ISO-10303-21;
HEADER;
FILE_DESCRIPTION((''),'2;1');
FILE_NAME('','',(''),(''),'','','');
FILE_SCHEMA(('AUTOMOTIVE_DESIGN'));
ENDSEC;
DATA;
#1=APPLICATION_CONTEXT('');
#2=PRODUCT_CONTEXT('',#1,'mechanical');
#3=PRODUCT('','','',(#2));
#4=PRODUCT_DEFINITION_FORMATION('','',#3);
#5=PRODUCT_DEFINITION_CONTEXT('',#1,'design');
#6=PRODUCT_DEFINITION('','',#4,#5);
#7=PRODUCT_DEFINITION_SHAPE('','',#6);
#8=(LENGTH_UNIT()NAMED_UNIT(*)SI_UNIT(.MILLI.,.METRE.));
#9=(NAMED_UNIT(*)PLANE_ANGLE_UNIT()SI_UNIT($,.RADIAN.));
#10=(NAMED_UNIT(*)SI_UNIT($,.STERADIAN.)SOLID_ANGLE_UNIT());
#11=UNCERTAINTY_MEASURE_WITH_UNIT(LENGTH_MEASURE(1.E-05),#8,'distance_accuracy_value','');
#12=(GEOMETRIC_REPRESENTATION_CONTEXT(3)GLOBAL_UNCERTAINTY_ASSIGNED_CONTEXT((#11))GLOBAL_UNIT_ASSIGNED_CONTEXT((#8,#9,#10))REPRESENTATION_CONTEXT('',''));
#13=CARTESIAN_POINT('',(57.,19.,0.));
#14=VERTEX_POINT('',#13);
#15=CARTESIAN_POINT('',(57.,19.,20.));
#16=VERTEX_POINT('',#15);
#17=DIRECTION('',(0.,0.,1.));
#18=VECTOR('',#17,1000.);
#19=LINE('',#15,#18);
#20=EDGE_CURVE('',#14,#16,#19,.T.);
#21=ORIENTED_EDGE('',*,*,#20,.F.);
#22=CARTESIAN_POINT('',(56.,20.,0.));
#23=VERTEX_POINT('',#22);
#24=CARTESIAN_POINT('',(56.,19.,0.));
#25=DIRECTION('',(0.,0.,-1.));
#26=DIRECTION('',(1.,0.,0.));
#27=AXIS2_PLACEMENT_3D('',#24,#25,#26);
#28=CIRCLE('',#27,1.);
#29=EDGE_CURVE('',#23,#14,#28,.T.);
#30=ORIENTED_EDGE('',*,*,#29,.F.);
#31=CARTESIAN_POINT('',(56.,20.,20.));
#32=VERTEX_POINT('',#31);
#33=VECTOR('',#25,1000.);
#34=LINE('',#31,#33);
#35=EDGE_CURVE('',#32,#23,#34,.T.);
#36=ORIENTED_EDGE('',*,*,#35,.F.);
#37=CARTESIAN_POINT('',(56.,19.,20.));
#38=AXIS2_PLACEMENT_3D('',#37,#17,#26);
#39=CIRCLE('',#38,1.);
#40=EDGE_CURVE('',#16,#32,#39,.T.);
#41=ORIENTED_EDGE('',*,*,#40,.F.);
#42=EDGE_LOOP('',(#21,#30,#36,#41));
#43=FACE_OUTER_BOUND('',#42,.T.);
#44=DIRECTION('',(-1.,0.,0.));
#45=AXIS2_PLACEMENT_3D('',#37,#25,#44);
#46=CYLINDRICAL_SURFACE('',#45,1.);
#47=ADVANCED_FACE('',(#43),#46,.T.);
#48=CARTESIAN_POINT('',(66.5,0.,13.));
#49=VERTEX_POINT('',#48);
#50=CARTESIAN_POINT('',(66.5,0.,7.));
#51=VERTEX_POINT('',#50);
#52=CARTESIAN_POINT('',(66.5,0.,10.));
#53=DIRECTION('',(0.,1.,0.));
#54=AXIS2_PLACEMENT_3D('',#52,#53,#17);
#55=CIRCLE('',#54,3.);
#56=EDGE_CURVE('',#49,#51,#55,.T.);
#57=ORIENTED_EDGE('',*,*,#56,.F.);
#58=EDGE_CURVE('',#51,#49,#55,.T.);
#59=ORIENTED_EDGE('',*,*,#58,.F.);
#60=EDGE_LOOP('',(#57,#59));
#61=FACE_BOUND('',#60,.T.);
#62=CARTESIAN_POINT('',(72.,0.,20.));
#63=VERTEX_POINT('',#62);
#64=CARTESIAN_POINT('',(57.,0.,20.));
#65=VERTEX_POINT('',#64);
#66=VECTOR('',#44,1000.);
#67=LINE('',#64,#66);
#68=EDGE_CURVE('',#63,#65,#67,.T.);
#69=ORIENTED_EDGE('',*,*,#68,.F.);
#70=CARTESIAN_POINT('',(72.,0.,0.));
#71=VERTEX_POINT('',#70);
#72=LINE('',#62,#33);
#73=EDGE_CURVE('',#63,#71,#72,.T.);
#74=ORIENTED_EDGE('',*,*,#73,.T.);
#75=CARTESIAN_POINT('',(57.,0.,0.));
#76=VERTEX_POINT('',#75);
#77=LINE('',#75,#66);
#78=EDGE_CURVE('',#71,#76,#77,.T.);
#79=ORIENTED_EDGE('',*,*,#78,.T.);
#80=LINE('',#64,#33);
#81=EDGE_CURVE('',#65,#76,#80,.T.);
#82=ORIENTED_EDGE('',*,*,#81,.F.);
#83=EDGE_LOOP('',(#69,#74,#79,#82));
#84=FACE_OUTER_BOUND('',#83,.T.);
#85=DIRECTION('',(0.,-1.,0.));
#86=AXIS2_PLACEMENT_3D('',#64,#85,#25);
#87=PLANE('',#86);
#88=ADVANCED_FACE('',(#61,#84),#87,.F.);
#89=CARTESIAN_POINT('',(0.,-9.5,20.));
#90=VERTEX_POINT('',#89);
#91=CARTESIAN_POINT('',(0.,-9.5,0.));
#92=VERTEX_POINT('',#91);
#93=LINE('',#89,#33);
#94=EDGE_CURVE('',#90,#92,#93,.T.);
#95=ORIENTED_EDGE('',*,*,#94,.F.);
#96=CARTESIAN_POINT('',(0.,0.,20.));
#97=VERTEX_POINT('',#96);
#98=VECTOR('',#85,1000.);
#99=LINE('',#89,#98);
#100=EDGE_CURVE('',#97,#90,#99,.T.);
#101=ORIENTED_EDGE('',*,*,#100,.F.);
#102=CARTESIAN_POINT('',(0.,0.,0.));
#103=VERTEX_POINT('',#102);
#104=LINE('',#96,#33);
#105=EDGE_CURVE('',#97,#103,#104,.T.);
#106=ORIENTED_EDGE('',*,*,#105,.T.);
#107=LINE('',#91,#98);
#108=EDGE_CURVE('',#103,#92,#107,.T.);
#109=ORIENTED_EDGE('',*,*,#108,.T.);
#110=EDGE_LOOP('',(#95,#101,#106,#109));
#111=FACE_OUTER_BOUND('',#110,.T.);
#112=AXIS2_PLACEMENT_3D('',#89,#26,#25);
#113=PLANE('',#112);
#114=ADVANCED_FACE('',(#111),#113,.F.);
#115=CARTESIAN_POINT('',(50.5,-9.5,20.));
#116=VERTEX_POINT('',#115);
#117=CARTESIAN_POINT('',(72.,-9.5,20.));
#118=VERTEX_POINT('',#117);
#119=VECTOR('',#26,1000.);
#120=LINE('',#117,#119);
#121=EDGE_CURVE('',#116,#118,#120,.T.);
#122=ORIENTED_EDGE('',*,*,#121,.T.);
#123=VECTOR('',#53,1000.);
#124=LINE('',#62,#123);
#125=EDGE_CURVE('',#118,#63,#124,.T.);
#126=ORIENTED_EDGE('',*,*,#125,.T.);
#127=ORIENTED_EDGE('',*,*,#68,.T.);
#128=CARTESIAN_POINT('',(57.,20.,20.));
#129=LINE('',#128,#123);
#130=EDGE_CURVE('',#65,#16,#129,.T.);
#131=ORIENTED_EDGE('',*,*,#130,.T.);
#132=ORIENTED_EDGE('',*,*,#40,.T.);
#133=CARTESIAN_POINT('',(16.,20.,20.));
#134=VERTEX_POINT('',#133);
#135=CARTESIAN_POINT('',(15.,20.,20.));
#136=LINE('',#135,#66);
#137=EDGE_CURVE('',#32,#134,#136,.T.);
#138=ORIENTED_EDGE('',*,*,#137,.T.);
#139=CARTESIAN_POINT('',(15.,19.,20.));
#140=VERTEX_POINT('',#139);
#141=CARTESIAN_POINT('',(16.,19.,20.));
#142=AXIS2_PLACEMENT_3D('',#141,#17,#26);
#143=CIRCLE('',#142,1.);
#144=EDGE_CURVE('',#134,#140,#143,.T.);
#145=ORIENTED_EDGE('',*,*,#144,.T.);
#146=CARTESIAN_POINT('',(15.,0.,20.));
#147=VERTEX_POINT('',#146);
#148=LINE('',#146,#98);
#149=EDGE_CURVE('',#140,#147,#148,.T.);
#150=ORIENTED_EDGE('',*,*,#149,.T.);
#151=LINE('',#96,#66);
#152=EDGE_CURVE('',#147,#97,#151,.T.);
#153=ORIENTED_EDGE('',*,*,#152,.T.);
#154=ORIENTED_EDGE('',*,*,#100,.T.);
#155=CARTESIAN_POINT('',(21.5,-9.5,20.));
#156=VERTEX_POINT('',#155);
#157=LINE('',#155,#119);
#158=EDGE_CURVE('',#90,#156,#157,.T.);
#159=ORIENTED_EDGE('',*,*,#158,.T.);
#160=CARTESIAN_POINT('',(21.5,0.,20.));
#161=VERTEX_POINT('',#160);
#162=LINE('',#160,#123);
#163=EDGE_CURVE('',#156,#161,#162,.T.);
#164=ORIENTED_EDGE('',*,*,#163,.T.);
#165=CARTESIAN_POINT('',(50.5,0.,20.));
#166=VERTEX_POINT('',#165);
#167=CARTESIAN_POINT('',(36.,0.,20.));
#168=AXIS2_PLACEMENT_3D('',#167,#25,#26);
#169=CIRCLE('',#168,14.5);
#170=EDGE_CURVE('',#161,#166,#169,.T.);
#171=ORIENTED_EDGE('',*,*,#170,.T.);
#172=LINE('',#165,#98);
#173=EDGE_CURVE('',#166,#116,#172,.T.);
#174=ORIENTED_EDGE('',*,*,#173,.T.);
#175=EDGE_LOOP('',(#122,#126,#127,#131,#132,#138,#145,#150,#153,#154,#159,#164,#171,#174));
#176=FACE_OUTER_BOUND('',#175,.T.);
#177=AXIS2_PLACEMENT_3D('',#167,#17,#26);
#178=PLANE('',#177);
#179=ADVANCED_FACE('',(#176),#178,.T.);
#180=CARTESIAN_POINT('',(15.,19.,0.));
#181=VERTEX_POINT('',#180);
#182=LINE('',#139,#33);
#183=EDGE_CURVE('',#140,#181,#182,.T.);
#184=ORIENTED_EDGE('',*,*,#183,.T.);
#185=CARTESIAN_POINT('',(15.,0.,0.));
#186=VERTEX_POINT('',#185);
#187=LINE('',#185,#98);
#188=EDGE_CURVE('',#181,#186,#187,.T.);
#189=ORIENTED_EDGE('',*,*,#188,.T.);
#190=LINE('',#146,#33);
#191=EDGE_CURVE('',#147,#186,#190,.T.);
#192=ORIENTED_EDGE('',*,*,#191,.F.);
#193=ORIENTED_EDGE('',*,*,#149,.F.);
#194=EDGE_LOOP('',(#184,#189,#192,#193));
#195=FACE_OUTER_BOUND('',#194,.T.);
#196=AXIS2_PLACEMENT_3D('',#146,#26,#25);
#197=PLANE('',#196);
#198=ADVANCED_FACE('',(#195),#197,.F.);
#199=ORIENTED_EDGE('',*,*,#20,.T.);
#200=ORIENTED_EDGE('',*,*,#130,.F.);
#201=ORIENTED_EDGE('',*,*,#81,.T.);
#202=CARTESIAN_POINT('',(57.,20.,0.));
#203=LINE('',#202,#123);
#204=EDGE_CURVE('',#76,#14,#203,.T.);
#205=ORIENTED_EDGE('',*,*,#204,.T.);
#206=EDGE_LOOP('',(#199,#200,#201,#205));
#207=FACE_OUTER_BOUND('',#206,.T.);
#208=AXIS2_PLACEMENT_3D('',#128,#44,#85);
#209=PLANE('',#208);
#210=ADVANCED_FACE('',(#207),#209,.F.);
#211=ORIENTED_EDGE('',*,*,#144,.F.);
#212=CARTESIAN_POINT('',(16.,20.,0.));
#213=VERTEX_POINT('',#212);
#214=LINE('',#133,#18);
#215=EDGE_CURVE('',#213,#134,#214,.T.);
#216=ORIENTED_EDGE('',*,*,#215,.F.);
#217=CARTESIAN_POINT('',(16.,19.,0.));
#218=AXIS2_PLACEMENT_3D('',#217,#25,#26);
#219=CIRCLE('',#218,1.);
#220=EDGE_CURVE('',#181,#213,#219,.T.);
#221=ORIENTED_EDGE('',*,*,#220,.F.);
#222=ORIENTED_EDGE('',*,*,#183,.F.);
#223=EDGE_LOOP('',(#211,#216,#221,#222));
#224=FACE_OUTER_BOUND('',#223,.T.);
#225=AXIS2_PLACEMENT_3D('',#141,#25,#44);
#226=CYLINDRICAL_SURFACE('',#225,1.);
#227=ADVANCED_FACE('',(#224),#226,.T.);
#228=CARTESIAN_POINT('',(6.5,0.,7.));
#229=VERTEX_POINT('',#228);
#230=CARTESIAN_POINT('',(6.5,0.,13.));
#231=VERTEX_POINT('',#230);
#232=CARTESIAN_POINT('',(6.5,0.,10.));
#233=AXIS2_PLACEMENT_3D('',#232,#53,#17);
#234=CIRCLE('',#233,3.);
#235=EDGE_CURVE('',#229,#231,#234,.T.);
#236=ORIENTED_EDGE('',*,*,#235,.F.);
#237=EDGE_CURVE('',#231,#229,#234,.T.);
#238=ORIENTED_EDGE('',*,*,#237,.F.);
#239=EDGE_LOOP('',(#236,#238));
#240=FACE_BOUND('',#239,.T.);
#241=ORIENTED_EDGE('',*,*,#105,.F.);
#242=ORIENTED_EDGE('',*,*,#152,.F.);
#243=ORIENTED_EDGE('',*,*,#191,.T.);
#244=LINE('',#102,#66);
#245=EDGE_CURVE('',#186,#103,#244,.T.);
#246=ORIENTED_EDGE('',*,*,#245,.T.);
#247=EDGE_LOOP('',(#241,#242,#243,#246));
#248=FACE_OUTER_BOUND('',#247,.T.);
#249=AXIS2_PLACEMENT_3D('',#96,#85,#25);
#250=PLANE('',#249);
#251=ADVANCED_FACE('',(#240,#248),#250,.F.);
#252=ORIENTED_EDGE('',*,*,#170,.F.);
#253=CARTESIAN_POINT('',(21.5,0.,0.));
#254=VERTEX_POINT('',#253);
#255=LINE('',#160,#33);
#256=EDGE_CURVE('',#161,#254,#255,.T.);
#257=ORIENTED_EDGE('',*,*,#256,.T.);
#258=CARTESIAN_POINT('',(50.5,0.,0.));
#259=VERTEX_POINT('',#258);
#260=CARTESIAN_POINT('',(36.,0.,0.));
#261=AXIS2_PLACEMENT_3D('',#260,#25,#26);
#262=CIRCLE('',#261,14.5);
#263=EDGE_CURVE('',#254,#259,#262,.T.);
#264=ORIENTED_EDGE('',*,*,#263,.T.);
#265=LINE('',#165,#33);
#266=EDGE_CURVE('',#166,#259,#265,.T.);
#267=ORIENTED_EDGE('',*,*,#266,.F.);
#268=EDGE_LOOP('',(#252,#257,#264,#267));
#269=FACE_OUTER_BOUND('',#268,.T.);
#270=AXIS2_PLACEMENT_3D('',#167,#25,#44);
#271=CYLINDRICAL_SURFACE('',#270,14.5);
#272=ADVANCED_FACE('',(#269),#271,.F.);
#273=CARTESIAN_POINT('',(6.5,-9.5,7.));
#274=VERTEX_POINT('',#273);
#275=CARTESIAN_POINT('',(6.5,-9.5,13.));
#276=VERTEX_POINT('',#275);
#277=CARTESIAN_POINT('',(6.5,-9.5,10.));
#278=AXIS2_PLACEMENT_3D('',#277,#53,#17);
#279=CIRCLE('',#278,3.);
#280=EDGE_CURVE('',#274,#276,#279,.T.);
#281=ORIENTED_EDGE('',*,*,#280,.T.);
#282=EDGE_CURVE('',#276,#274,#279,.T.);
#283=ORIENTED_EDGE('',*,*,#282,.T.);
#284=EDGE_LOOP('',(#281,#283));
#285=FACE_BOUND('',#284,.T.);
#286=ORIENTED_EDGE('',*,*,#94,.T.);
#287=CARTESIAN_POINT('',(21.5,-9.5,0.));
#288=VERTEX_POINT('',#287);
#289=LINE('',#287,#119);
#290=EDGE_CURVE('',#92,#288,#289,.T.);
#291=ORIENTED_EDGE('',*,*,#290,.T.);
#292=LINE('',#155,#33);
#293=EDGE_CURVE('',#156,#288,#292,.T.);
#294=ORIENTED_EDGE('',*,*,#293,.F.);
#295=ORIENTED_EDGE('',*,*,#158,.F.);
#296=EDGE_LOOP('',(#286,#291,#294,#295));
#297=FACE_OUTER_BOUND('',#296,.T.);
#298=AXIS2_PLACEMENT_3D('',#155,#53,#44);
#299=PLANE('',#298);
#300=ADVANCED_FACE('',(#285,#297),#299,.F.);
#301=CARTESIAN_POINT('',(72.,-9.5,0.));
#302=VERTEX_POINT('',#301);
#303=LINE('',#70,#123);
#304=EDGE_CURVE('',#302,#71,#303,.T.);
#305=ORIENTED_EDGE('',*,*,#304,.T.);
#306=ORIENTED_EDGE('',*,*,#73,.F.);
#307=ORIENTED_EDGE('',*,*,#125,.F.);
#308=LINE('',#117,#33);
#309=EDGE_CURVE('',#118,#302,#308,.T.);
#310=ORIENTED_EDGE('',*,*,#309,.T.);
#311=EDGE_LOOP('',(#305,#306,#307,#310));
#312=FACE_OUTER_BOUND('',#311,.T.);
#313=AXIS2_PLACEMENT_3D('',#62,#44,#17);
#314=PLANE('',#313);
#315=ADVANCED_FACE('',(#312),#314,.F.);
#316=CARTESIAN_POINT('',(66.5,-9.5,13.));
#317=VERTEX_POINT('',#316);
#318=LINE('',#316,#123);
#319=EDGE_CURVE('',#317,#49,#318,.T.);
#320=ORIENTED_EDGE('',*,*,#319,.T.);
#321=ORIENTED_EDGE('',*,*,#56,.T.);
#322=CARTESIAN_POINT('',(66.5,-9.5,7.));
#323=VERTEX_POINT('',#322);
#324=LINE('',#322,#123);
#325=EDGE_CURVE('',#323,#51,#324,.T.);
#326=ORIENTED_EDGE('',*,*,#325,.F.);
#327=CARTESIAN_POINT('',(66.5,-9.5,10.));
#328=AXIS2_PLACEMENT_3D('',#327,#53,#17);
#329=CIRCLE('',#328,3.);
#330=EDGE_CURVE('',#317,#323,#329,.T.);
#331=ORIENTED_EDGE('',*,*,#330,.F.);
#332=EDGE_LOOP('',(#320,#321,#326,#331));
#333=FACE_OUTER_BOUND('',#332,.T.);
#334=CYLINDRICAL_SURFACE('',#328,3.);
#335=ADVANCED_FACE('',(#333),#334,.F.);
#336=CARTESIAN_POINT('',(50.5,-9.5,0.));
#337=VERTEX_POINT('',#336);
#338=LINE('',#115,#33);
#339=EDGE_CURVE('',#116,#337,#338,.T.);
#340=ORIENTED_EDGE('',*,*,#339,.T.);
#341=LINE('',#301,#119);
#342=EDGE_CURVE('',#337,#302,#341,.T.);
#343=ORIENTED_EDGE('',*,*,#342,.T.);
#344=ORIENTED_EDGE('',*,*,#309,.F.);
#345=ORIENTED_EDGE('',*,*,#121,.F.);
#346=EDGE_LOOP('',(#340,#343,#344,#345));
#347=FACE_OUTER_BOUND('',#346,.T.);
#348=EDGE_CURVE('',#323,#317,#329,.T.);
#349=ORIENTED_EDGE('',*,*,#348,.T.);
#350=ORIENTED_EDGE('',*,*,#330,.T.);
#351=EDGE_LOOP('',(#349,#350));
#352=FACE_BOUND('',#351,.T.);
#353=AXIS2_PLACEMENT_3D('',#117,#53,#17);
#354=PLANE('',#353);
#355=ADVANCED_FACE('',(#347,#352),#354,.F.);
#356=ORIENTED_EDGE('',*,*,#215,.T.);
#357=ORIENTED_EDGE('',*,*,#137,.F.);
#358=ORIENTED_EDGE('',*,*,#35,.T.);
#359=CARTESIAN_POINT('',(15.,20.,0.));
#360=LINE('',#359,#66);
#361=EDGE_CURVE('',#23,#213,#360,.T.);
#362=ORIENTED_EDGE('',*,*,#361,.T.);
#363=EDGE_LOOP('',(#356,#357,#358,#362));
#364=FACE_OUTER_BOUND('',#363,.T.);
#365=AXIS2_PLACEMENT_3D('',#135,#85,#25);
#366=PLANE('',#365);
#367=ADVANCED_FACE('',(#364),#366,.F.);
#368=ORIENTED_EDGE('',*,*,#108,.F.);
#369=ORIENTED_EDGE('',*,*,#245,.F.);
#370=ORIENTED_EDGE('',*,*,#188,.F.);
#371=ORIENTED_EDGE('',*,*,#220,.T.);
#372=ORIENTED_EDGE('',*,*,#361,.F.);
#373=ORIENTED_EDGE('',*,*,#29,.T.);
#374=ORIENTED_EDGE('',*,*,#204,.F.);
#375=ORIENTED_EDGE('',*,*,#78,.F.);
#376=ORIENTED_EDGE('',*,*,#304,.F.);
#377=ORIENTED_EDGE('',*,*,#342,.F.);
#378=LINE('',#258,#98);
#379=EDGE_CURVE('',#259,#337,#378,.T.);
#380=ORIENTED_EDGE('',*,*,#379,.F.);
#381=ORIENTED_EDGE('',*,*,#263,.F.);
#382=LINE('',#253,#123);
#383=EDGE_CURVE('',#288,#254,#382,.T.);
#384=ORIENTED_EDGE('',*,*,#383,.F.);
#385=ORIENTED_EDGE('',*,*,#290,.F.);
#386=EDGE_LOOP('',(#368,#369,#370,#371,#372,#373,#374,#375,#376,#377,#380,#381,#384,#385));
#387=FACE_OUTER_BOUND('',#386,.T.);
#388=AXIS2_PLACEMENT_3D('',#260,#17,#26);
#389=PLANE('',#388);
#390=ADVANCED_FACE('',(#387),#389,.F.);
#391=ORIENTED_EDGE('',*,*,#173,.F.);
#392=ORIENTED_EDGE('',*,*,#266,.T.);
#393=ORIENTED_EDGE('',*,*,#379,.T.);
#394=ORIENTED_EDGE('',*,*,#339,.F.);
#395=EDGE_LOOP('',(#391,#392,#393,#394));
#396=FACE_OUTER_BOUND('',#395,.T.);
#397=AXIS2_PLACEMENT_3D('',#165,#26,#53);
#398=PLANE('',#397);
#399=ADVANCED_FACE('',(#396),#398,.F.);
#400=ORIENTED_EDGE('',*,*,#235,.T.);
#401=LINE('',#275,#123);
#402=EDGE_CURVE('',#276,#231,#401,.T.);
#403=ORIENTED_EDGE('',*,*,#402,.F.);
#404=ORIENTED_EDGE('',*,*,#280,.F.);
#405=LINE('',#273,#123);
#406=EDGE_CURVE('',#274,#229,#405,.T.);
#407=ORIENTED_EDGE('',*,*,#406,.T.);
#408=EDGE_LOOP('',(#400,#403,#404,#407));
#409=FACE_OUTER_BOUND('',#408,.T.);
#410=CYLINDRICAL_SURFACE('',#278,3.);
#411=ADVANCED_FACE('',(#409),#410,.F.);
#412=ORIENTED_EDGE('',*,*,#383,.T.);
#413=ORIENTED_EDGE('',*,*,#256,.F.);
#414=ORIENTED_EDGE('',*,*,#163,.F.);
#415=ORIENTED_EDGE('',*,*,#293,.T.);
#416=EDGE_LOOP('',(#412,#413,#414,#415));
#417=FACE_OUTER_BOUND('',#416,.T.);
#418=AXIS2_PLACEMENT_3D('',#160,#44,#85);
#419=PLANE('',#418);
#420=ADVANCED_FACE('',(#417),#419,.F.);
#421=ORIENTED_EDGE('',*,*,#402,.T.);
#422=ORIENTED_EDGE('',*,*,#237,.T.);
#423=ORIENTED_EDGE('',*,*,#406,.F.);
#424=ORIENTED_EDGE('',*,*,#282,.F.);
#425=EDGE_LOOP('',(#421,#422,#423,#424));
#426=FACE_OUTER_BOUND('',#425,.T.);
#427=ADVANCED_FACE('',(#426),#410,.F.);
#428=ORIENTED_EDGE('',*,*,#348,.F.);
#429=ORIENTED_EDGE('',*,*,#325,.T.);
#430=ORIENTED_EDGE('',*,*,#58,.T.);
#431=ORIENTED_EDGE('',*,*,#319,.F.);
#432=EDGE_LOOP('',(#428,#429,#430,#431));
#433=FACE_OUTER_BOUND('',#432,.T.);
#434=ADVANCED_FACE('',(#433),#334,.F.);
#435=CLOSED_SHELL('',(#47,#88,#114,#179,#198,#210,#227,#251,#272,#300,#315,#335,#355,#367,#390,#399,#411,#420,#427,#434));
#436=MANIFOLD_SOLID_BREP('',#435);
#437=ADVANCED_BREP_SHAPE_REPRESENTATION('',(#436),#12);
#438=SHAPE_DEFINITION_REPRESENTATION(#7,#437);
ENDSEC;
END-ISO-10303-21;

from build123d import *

# Parameters (mm, degrees)
EXTRUDE_1_DEPTH     = 20
FILLET_1_R          = 1
SKETCH_2_R          = 3
CUT_EXTRUDE_1_DEPTH = 78.356318423


with BuildPart() as part:
    # 草图1 → 凸台-拉伸1 (new body)
    with BuildSketch(Plane.XY):
        with BuildLine():
            Line((0, 0), (15, 0))
            Line((15, 0), (15, 20))
            Line((15, 20), (57, 20))
            Line((57, 20), (57, 0))
            Line((57, 0), (72, 0))
            Line((72, 0), (72, -9.5))
            Line((72, -9.5), (50.5, -9.5))
            Line((50.5, -9.5), (50.5, 0))
            ThreePointArc((50.5, 0), (36, 14.5), (21.5, 0))
            Line((21.5, 0), (21.5, -9.5))
            Line((21.5, -9.5), (0, -9.5))
            Line((0, -9.5), (0, 0))
        make_face()
    extrude(amount=EXTRUDE_1_DEPTH)

    # 圆角1
    fillet_1_edges = [part.edges().sort_by_distance(p)[0] for p in [
        (15, 20, 10),
        (57, 20, 10),
    ]]
    fillet(fillet_1_edges, radius=FILLET_1_R)

    # 草图2 → 切除-拉伸1 (cut, through all)
    with BuildSketch(Plane(origin=(0, 0, 0), x_dir=(1, 0, 0), z_dir=(0, 1, 0))):
        with Locations(Location((6.5, -10, 0), (0, 0, 270))):
            Circle(SKETCH_2_R)
        with Locations(Location((66.5, -10, 0), (0, 0, 270))):
            Circle(SKETCH_2_R)
    extrude(amount=-CUT_EXTRUDE_1_DEPTH, mode=Mode.SUBTRACT)


solid = part.part
